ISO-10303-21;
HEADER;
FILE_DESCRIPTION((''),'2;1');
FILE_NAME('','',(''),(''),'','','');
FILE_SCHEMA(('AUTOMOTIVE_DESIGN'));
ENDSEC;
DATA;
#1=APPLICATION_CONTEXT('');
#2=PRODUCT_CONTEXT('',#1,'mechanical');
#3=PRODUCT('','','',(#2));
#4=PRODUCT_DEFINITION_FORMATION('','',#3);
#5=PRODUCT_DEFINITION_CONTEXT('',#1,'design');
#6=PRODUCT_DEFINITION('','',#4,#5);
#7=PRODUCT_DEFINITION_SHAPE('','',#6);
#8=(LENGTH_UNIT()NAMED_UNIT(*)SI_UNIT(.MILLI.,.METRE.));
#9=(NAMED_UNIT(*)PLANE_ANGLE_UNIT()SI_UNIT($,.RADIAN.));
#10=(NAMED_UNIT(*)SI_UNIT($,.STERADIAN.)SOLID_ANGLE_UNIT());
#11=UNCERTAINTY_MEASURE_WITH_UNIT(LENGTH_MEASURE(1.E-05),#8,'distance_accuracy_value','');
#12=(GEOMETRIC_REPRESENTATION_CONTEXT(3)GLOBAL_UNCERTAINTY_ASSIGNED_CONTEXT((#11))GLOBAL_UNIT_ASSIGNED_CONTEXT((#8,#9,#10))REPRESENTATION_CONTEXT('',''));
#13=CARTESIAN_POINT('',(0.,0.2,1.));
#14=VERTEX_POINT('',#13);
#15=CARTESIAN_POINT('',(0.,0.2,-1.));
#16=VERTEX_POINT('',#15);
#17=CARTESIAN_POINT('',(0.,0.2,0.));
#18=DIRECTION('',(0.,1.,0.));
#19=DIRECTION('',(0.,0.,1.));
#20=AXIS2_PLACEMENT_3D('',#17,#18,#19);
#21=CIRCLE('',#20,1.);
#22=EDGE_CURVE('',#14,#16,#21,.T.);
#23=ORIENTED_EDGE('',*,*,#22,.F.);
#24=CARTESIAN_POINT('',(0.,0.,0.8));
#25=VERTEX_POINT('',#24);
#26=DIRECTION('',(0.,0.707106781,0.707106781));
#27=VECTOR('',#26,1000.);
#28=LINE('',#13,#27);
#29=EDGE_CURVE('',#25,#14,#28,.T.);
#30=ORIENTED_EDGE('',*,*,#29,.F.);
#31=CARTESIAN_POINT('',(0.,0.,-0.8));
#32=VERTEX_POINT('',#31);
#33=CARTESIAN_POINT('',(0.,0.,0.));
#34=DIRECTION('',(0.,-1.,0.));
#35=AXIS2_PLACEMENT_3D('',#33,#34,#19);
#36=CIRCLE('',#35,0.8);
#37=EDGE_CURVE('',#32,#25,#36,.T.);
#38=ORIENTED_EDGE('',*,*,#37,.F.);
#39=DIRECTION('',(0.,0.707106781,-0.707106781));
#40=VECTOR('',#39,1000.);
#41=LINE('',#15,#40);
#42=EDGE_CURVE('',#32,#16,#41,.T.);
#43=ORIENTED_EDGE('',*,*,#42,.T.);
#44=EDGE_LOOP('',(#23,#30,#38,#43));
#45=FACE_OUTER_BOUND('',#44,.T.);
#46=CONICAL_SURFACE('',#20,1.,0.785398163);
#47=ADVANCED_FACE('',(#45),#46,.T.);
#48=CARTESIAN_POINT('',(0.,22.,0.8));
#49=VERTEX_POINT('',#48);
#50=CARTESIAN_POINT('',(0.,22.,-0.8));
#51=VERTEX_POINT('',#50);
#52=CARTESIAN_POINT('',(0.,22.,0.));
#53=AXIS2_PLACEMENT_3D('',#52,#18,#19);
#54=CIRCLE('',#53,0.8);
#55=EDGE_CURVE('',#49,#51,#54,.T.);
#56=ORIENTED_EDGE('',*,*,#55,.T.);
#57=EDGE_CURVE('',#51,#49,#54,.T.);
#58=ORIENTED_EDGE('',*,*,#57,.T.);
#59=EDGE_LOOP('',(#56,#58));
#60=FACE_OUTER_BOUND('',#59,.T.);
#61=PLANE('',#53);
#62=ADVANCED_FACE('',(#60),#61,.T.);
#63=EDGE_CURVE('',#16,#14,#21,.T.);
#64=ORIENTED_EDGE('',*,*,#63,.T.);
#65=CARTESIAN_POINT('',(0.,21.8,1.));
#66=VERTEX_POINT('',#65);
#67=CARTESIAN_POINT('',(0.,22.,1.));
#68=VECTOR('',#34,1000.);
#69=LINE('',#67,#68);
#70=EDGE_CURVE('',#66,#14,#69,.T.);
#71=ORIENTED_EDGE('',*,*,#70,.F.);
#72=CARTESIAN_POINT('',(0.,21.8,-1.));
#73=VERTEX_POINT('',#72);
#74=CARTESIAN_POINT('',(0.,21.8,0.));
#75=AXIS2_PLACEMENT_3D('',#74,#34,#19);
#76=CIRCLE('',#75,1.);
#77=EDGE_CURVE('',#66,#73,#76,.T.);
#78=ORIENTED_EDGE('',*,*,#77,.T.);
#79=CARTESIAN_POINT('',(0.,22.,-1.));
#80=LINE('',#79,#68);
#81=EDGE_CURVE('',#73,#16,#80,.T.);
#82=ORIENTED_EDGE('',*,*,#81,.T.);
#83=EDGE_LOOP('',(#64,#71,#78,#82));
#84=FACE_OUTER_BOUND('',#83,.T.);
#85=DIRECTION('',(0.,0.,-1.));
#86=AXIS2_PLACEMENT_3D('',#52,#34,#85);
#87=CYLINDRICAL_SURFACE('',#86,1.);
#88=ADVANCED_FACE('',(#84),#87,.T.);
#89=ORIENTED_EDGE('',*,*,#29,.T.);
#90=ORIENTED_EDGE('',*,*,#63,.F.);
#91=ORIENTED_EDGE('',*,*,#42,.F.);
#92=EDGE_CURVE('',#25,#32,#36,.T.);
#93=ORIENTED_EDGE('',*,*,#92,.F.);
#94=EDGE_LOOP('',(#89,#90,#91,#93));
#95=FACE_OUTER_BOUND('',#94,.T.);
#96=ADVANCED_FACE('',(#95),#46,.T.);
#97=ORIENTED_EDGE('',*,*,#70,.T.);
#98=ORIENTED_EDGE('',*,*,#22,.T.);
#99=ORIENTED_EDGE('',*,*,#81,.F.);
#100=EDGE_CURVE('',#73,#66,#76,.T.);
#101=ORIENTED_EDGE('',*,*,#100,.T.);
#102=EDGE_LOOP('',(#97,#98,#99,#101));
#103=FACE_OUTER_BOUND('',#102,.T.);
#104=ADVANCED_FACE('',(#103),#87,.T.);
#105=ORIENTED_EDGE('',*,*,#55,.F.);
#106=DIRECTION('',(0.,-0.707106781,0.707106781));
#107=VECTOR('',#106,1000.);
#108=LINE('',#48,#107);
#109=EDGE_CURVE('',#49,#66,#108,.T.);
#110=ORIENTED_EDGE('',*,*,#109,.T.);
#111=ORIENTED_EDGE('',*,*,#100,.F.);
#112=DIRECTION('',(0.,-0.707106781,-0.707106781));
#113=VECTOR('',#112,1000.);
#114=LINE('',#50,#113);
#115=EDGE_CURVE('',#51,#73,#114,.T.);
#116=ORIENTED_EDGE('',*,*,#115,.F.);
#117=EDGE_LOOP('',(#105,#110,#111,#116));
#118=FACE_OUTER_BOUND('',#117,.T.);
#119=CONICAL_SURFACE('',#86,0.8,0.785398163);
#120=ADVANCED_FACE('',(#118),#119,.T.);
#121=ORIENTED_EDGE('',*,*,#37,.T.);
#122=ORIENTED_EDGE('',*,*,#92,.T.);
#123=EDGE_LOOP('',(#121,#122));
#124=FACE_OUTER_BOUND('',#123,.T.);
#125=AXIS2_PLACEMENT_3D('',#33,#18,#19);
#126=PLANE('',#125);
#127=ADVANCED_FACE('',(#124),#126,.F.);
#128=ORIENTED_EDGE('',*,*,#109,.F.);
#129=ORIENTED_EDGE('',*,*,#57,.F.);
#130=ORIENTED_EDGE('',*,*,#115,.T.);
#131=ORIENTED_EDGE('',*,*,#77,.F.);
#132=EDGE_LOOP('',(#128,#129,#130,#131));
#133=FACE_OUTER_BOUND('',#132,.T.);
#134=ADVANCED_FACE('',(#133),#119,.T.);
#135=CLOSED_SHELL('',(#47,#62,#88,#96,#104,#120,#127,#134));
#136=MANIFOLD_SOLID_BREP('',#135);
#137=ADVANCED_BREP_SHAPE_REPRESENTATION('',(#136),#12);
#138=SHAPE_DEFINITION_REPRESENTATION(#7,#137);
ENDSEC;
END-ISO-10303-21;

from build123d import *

# Parameters (mm, degrees)
SKETCH_1_R          = 1
EXTRUDE_1_DEPTH     = 22
CHAMFER_C0_2_1_SIZE = 0.2


with BuildPart() as part:
    # 草图1 → 凸台-拉伸1 (new body)
    with BuildSketch(Plane(origin=(0, 0, 0), x_dir=(1, 0, 0), z_dir=(0, 1, 0))):
        with Locations(Location((0, 0, 0), (0, 0, 270))):
            Circle(SKETCH_1_R)
    extrude(amount=EXTRUDE_1_DEPTH)

    # C0.2 倒角1
    chamfer_c0_2_1_edges = [part.edges().sort_by_distance(p)[0] for p in [
        (0, 0, -1),
        (0, 22, -1),
    ]]
    chamfer(chamfer_c0_2_1_edges, length=CHAMFER_C0_2_1_SIZE)


solid = part.part
